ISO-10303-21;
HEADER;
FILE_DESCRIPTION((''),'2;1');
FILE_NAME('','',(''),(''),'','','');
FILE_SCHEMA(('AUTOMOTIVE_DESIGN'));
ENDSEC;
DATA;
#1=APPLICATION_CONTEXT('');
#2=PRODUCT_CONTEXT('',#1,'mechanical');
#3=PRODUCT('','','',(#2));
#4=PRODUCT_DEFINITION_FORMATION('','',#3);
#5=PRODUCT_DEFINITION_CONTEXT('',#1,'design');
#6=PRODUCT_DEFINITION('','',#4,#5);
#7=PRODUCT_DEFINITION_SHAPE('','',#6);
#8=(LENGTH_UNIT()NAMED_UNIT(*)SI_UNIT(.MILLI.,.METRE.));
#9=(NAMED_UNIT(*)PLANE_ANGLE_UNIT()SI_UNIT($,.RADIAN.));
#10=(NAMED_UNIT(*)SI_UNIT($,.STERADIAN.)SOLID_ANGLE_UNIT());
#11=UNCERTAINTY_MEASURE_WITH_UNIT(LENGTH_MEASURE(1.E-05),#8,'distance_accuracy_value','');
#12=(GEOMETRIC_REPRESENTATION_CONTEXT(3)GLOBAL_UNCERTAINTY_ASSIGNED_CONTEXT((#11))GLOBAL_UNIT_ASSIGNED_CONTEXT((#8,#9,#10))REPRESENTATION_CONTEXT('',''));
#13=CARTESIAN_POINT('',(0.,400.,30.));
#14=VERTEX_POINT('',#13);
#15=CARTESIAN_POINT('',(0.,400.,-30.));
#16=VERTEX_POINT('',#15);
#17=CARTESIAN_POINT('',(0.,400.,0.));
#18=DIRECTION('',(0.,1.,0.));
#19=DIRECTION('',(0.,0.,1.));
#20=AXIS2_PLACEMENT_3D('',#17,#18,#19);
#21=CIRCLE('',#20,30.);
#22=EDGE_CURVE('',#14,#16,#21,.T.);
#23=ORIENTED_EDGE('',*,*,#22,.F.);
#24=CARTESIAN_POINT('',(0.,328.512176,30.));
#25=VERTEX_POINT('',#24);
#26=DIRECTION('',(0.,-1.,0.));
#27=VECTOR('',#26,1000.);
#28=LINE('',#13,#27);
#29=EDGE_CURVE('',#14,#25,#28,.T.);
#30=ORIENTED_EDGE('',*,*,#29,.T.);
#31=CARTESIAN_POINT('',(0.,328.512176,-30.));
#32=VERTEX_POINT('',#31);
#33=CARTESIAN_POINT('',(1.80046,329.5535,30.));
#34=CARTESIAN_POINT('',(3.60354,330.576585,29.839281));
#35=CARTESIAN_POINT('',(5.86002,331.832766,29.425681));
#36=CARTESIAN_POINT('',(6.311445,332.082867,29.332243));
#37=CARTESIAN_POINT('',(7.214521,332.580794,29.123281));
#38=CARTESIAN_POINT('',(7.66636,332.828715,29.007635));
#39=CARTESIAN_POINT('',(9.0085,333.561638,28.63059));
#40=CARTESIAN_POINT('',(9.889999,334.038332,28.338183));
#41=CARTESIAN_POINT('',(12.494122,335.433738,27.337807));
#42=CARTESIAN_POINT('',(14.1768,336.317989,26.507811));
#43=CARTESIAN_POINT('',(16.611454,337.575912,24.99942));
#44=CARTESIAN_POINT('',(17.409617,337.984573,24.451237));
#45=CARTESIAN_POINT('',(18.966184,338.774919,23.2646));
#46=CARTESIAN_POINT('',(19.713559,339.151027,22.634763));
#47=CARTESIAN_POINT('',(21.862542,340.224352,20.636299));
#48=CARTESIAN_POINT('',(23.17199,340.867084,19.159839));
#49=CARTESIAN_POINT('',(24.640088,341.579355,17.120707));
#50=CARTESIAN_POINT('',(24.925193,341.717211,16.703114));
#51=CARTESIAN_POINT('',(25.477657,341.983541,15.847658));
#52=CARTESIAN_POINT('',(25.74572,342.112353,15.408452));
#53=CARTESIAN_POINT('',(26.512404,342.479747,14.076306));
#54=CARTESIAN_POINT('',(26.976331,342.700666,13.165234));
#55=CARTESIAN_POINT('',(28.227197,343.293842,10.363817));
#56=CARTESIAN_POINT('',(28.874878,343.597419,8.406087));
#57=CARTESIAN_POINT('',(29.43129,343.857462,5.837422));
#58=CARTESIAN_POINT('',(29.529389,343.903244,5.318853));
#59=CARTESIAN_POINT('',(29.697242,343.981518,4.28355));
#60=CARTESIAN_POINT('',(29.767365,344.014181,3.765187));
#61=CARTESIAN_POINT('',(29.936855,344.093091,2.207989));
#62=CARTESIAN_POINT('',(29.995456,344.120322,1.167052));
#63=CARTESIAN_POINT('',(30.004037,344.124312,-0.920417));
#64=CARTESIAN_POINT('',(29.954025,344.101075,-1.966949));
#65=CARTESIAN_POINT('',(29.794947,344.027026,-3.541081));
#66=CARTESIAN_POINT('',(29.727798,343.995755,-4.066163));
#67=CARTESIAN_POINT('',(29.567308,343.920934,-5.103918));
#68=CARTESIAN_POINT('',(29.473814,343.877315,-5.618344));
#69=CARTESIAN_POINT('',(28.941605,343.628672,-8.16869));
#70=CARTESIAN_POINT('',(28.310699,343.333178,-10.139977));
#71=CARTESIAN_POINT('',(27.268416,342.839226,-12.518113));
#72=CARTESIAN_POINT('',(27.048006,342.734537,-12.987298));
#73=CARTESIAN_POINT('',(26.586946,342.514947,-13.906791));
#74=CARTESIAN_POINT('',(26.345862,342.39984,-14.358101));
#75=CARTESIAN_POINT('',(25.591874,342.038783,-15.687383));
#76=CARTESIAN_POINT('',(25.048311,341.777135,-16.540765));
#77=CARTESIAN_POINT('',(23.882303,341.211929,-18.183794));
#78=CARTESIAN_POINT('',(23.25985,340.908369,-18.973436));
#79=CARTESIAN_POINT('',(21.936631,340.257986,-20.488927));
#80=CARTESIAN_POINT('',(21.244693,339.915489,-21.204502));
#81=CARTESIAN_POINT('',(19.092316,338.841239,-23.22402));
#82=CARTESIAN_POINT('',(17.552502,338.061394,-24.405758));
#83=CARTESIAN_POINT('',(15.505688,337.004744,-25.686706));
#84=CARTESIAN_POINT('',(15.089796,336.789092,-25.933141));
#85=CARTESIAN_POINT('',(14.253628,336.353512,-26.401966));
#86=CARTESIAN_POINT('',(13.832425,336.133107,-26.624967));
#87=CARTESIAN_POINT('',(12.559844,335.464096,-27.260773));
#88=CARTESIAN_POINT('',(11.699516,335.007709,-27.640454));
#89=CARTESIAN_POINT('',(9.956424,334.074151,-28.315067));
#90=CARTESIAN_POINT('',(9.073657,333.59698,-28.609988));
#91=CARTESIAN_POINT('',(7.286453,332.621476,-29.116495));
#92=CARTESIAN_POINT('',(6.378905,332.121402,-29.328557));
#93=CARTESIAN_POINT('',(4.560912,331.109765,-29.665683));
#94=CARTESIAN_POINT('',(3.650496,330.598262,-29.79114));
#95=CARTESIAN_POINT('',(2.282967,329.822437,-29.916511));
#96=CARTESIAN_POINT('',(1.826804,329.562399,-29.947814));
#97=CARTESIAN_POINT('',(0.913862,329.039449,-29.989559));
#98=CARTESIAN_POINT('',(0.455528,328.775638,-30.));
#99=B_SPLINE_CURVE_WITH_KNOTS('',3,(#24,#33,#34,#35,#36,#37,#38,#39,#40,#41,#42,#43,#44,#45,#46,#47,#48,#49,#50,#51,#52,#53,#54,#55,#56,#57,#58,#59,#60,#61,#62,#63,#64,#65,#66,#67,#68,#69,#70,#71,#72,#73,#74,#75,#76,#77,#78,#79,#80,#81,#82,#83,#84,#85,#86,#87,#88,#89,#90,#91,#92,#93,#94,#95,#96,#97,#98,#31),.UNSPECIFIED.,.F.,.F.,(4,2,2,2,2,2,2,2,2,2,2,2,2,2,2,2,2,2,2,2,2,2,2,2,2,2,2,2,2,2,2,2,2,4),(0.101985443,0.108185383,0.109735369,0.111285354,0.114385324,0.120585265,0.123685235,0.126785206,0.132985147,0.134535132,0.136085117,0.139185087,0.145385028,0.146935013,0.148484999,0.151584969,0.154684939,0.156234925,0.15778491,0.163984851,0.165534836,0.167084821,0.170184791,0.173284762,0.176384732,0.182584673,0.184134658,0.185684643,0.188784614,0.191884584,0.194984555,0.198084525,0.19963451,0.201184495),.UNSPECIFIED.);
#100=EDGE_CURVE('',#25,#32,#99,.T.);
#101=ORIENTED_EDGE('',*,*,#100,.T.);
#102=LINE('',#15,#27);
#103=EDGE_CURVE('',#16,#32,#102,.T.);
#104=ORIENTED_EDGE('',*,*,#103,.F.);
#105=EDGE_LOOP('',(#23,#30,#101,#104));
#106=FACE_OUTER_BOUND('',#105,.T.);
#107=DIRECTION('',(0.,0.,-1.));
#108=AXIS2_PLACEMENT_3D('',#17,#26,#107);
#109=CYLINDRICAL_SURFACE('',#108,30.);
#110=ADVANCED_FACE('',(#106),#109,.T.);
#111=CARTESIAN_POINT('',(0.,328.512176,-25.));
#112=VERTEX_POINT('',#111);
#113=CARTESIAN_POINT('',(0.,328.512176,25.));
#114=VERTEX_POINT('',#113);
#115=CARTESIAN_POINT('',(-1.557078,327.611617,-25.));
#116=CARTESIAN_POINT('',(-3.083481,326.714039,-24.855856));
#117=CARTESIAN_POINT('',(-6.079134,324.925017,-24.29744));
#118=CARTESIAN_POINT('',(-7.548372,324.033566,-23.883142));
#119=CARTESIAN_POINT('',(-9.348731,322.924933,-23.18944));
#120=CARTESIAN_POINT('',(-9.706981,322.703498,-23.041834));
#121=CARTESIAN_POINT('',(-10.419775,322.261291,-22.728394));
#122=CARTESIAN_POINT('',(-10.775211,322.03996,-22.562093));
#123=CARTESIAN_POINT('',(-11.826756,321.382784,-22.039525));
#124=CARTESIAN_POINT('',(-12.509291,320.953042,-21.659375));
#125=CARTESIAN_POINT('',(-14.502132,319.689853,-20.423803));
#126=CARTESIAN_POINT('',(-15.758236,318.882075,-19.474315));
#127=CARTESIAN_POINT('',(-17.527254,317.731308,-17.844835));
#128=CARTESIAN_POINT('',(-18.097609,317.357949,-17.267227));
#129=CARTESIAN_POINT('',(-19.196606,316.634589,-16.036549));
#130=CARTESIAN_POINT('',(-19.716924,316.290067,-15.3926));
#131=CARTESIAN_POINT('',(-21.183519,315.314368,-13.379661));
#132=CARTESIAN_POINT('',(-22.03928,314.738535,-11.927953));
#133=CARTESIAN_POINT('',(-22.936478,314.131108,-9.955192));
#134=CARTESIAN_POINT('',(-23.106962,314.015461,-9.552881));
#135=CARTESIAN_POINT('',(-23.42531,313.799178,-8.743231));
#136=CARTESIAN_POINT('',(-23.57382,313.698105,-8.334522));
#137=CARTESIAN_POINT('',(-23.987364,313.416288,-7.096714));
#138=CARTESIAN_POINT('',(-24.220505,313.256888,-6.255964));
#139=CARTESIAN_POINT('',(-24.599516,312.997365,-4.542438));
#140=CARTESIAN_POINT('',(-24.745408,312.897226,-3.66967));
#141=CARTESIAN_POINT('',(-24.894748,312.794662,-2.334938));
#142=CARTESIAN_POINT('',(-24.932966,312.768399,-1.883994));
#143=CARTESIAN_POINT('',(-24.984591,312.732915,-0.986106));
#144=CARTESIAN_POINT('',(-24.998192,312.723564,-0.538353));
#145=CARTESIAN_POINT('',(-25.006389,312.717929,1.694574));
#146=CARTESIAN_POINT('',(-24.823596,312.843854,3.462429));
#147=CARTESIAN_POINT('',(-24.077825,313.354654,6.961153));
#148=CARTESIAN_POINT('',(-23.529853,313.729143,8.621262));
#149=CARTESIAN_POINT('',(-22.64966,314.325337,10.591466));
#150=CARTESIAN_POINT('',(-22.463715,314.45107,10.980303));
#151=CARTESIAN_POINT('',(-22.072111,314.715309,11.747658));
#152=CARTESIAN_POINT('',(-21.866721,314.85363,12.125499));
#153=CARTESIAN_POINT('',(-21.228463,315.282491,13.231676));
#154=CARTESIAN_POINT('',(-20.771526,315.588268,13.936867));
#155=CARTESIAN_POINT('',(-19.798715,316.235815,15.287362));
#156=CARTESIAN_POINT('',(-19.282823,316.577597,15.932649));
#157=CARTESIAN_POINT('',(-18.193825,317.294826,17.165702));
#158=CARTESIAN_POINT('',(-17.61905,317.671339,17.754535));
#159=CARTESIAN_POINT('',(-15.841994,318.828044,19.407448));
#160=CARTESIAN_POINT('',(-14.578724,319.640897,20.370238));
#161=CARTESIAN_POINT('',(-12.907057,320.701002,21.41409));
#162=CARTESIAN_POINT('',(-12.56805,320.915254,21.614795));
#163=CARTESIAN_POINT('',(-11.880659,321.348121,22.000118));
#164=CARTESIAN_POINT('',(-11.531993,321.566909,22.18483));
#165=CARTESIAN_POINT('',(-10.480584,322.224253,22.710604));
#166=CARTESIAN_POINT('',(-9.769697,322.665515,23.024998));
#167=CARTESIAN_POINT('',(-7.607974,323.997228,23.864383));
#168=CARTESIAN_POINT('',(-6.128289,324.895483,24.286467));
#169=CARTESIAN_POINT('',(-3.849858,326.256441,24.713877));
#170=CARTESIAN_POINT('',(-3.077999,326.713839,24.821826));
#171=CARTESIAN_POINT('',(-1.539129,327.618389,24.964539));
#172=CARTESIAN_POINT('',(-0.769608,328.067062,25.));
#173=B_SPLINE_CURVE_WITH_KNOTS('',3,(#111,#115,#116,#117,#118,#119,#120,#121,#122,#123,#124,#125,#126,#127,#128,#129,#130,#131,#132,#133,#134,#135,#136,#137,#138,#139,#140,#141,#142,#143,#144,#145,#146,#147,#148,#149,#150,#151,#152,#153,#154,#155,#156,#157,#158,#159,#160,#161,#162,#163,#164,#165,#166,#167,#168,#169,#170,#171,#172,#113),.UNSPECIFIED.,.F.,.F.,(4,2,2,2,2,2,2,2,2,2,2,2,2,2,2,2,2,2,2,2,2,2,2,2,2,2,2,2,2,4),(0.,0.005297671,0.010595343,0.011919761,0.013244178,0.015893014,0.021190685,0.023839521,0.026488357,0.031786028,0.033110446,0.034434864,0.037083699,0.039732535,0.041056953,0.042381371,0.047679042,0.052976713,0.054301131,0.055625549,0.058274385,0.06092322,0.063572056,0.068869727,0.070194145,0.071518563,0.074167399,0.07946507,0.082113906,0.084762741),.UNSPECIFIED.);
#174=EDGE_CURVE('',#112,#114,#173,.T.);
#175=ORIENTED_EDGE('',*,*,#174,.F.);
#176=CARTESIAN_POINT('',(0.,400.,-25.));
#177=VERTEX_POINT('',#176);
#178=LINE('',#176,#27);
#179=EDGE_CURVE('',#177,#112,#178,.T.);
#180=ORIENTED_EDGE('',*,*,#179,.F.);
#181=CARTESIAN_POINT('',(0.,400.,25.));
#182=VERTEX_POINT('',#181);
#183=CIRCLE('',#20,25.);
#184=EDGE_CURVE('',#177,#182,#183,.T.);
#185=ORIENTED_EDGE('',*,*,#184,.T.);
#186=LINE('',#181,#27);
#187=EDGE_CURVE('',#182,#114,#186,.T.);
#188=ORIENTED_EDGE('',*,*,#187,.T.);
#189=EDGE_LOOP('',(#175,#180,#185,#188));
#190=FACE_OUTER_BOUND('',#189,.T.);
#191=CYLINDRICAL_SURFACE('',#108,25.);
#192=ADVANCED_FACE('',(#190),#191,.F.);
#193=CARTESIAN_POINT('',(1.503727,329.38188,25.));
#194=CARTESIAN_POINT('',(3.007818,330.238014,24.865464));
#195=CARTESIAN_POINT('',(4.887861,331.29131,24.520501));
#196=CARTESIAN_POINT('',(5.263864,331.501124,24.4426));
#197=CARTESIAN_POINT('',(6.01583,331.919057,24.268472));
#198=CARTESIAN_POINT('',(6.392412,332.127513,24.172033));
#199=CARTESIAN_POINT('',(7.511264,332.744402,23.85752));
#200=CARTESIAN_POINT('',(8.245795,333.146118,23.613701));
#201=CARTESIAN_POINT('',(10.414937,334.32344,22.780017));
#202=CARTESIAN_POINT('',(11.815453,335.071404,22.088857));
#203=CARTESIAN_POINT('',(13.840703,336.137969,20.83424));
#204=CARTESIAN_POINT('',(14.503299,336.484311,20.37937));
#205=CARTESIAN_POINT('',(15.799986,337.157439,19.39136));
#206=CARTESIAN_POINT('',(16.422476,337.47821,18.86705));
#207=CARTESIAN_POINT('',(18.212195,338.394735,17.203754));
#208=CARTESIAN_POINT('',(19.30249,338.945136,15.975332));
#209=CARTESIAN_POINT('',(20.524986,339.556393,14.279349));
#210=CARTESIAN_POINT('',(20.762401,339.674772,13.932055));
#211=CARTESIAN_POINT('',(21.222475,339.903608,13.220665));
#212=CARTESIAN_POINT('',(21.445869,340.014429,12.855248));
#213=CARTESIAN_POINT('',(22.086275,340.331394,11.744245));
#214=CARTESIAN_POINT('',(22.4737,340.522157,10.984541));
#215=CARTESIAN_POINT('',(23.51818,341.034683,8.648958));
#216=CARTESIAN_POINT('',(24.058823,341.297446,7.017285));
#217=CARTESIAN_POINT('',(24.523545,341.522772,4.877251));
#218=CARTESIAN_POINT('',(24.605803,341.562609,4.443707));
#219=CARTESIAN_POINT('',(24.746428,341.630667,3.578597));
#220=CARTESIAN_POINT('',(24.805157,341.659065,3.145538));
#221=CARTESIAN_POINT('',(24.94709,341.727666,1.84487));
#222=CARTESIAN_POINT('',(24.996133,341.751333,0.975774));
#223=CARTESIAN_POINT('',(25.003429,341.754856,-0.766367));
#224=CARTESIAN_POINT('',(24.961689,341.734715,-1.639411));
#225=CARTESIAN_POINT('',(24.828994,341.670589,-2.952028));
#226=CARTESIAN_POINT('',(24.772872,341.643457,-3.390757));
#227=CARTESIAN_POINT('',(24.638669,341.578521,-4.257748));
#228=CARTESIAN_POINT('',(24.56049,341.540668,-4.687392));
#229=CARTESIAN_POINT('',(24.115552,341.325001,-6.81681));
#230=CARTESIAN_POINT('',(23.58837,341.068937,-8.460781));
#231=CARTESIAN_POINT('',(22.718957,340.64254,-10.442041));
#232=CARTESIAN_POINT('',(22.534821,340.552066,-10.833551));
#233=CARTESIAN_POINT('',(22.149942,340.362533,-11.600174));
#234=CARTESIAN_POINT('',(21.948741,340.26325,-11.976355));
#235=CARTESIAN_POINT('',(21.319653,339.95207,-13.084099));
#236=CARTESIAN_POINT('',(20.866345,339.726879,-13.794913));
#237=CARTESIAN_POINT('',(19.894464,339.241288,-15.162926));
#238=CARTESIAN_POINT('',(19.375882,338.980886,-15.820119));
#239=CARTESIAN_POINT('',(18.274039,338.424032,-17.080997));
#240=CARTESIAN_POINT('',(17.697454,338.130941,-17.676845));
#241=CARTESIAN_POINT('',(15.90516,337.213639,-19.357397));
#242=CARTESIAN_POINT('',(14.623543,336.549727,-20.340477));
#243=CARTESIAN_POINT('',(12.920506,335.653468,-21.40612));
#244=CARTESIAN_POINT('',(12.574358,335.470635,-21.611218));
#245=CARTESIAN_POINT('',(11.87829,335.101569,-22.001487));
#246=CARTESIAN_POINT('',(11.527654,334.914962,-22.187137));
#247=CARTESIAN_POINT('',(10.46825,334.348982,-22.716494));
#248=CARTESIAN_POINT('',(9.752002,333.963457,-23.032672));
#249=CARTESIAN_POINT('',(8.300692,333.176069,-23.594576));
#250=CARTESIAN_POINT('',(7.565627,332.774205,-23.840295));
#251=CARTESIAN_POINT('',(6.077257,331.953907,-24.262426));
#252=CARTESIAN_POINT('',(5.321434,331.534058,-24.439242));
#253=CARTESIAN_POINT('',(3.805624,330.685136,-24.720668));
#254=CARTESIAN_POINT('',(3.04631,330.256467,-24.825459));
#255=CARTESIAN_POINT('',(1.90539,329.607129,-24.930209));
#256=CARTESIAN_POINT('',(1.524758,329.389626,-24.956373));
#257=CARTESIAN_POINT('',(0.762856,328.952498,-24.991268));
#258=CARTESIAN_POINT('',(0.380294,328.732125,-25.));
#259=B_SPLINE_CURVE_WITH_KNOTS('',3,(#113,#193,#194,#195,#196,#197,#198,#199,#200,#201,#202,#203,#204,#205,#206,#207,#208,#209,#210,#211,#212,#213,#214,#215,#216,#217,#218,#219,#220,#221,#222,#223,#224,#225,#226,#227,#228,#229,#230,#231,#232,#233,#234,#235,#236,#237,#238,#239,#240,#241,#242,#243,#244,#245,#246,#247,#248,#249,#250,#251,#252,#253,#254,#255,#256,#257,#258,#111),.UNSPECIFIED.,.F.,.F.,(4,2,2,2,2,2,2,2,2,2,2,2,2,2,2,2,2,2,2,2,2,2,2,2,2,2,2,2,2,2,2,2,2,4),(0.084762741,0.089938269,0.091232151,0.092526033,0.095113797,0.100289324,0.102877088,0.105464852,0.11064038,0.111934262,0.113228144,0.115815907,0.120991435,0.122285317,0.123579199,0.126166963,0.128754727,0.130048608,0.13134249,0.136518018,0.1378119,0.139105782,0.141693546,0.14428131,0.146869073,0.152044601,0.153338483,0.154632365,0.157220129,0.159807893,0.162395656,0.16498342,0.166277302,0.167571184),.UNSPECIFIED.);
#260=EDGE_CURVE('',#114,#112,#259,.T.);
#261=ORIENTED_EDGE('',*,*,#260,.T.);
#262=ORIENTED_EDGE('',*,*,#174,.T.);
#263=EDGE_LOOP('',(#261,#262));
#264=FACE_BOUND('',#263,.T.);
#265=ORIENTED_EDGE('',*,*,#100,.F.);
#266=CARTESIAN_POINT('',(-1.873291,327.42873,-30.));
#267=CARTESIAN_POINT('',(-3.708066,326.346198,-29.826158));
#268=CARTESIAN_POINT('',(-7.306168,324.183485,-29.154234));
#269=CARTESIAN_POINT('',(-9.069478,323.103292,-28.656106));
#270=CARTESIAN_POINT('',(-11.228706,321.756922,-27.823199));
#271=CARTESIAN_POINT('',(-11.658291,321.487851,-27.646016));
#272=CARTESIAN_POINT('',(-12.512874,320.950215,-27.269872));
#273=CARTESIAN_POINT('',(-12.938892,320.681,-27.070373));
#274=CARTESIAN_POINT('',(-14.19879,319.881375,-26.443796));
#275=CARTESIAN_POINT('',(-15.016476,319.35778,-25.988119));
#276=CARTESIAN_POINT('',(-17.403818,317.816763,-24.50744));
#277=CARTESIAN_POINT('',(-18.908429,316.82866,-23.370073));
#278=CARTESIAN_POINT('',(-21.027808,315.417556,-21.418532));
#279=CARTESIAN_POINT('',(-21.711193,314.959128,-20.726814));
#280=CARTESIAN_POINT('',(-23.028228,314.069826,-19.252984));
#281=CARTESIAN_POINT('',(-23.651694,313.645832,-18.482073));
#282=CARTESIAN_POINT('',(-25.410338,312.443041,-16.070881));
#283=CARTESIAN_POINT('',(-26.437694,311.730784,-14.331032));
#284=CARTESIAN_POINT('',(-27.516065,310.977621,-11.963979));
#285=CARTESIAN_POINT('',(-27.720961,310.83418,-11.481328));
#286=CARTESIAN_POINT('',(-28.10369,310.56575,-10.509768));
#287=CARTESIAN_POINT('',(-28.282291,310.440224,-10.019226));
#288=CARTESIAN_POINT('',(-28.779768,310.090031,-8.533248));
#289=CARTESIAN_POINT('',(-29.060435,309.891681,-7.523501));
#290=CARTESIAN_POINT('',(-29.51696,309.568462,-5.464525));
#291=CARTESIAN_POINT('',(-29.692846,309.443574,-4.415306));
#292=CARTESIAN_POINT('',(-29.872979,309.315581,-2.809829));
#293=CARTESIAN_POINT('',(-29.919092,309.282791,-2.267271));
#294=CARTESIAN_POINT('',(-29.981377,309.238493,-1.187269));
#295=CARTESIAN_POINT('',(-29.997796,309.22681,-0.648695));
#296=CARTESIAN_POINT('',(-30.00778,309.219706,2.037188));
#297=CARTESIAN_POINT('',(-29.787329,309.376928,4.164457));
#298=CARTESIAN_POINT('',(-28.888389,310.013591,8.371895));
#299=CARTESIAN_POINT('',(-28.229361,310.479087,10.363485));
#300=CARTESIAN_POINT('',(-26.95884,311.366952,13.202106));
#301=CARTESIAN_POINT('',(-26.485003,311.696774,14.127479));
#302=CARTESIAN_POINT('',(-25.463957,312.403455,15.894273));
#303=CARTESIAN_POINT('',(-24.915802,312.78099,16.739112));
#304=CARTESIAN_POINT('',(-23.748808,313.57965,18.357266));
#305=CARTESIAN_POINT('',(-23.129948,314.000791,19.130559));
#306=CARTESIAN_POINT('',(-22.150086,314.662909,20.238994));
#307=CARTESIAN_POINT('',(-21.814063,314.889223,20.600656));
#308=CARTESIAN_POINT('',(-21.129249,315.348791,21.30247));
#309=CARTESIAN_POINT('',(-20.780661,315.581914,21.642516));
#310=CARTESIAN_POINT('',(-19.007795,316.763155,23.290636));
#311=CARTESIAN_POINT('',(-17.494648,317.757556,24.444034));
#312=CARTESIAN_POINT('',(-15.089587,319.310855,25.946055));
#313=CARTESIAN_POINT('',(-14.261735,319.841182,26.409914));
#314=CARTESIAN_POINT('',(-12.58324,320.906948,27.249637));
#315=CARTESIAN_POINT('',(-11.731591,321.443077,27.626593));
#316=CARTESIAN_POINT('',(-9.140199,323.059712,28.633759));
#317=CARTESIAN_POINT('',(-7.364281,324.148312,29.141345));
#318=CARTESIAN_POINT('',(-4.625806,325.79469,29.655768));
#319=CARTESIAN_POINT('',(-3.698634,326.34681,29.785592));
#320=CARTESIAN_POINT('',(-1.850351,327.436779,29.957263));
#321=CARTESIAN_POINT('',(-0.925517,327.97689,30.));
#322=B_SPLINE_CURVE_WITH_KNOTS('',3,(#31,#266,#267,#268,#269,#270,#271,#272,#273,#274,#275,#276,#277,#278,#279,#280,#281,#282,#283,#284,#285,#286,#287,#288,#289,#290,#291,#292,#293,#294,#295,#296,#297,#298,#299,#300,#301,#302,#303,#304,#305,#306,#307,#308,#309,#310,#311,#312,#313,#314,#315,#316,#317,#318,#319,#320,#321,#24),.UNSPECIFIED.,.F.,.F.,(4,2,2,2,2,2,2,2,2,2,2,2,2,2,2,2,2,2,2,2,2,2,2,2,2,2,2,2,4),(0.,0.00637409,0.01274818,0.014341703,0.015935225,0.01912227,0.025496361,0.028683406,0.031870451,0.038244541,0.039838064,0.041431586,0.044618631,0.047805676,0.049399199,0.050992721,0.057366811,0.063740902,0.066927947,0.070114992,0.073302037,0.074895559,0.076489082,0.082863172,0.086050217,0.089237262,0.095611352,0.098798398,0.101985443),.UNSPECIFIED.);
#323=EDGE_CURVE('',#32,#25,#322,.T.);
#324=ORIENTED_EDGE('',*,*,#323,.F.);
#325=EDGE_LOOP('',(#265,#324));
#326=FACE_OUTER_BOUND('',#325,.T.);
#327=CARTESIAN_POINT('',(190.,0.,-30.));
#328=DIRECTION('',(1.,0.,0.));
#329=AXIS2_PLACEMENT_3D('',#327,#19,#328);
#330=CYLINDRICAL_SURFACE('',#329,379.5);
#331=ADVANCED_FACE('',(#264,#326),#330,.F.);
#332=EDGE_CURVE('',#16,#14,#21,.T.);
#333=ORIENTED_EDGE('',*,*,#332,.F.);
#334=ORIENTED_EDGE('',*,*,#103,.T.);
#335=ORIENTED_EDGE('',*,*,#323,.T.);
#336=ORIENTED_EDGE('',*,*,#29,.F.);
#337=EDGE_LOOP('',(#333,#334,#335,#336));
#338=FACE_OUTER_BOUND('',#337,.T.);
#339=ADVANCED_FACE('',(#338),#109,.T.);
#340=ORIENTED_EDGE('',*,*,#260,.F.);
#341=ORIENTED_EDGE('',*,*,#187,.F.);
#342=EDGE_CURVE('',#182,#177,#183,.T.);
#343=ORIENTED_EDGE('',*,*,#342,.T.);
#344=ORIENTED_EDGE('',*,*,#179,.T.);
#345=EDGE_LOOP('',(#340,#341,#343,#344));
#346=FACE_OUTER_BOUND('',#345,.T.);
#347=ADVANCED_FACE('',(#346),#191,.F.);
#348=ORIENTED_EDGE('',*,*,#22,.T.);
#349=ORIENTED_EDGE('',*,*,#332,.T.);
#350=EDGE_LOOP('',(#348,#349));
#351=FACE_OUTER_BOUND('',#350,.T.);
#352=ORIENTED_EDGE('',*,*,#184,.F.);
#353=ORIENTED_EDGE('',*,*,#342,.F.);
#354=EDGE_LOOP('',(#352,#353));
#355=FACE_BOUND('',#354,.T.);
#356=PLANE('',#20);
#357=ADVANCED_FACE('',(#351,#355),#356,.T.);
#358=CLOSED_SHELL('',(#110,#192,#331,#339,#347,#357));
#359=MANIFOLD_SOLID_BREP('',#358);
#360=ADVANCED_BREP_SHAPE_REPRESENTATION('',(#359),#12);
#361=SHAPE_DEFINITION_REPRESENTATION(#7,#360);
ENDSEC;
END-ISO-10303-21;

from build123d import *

# Parameters (mm, degrees)
SKETCH2_R               = 30
SKETCH2_R_2             = 25
BOSS_EXTRUDE1_DEPTH     = 400
CUT_EXTRUDE1_DEPTH      = 403.243707222
CUT_EXTRUDE1_DEPTH_BACK = 403.243707222
SKETCH3_R               = 379.5


with BuildPart() as part:
    # Sketch2 → Boss-Extrude1 (new body)
    with BuildSketch(Plane(origin=(0, 0, 0), x_dir=(1, 0, 0), z_dir=(0, 1, 0))):
        with Locations(Location((0, 0, 0), (0, 0, 270))):
            Circle(SKETCH2_R)
        with Locations(Location((0, 0, 0), (0, 0, 270))):
            Circle(SKETCH2_R_2, mode=Mode.SUBTRACT)
    extrude(amount=BOSS_EXTRUDE1_DEPTH)

    # Sketch3 → Cut-Extrude1 (cut, two sides: drawn at the far end of the back side and taken through both)
    with BuildSketch(Plane.XY.offset(-CUT_EXTRUDE1_DEPTH_BACK)):
        with Locations((190, 0)):
            Circle(SKETCH3_R)
    extrude(amount=CUT_EXTRUDE1_DEPTH + CUT_EXTRUDE1_DEPTH_BACK, mode=Mode.SUBTRACT)


solid = part.part
